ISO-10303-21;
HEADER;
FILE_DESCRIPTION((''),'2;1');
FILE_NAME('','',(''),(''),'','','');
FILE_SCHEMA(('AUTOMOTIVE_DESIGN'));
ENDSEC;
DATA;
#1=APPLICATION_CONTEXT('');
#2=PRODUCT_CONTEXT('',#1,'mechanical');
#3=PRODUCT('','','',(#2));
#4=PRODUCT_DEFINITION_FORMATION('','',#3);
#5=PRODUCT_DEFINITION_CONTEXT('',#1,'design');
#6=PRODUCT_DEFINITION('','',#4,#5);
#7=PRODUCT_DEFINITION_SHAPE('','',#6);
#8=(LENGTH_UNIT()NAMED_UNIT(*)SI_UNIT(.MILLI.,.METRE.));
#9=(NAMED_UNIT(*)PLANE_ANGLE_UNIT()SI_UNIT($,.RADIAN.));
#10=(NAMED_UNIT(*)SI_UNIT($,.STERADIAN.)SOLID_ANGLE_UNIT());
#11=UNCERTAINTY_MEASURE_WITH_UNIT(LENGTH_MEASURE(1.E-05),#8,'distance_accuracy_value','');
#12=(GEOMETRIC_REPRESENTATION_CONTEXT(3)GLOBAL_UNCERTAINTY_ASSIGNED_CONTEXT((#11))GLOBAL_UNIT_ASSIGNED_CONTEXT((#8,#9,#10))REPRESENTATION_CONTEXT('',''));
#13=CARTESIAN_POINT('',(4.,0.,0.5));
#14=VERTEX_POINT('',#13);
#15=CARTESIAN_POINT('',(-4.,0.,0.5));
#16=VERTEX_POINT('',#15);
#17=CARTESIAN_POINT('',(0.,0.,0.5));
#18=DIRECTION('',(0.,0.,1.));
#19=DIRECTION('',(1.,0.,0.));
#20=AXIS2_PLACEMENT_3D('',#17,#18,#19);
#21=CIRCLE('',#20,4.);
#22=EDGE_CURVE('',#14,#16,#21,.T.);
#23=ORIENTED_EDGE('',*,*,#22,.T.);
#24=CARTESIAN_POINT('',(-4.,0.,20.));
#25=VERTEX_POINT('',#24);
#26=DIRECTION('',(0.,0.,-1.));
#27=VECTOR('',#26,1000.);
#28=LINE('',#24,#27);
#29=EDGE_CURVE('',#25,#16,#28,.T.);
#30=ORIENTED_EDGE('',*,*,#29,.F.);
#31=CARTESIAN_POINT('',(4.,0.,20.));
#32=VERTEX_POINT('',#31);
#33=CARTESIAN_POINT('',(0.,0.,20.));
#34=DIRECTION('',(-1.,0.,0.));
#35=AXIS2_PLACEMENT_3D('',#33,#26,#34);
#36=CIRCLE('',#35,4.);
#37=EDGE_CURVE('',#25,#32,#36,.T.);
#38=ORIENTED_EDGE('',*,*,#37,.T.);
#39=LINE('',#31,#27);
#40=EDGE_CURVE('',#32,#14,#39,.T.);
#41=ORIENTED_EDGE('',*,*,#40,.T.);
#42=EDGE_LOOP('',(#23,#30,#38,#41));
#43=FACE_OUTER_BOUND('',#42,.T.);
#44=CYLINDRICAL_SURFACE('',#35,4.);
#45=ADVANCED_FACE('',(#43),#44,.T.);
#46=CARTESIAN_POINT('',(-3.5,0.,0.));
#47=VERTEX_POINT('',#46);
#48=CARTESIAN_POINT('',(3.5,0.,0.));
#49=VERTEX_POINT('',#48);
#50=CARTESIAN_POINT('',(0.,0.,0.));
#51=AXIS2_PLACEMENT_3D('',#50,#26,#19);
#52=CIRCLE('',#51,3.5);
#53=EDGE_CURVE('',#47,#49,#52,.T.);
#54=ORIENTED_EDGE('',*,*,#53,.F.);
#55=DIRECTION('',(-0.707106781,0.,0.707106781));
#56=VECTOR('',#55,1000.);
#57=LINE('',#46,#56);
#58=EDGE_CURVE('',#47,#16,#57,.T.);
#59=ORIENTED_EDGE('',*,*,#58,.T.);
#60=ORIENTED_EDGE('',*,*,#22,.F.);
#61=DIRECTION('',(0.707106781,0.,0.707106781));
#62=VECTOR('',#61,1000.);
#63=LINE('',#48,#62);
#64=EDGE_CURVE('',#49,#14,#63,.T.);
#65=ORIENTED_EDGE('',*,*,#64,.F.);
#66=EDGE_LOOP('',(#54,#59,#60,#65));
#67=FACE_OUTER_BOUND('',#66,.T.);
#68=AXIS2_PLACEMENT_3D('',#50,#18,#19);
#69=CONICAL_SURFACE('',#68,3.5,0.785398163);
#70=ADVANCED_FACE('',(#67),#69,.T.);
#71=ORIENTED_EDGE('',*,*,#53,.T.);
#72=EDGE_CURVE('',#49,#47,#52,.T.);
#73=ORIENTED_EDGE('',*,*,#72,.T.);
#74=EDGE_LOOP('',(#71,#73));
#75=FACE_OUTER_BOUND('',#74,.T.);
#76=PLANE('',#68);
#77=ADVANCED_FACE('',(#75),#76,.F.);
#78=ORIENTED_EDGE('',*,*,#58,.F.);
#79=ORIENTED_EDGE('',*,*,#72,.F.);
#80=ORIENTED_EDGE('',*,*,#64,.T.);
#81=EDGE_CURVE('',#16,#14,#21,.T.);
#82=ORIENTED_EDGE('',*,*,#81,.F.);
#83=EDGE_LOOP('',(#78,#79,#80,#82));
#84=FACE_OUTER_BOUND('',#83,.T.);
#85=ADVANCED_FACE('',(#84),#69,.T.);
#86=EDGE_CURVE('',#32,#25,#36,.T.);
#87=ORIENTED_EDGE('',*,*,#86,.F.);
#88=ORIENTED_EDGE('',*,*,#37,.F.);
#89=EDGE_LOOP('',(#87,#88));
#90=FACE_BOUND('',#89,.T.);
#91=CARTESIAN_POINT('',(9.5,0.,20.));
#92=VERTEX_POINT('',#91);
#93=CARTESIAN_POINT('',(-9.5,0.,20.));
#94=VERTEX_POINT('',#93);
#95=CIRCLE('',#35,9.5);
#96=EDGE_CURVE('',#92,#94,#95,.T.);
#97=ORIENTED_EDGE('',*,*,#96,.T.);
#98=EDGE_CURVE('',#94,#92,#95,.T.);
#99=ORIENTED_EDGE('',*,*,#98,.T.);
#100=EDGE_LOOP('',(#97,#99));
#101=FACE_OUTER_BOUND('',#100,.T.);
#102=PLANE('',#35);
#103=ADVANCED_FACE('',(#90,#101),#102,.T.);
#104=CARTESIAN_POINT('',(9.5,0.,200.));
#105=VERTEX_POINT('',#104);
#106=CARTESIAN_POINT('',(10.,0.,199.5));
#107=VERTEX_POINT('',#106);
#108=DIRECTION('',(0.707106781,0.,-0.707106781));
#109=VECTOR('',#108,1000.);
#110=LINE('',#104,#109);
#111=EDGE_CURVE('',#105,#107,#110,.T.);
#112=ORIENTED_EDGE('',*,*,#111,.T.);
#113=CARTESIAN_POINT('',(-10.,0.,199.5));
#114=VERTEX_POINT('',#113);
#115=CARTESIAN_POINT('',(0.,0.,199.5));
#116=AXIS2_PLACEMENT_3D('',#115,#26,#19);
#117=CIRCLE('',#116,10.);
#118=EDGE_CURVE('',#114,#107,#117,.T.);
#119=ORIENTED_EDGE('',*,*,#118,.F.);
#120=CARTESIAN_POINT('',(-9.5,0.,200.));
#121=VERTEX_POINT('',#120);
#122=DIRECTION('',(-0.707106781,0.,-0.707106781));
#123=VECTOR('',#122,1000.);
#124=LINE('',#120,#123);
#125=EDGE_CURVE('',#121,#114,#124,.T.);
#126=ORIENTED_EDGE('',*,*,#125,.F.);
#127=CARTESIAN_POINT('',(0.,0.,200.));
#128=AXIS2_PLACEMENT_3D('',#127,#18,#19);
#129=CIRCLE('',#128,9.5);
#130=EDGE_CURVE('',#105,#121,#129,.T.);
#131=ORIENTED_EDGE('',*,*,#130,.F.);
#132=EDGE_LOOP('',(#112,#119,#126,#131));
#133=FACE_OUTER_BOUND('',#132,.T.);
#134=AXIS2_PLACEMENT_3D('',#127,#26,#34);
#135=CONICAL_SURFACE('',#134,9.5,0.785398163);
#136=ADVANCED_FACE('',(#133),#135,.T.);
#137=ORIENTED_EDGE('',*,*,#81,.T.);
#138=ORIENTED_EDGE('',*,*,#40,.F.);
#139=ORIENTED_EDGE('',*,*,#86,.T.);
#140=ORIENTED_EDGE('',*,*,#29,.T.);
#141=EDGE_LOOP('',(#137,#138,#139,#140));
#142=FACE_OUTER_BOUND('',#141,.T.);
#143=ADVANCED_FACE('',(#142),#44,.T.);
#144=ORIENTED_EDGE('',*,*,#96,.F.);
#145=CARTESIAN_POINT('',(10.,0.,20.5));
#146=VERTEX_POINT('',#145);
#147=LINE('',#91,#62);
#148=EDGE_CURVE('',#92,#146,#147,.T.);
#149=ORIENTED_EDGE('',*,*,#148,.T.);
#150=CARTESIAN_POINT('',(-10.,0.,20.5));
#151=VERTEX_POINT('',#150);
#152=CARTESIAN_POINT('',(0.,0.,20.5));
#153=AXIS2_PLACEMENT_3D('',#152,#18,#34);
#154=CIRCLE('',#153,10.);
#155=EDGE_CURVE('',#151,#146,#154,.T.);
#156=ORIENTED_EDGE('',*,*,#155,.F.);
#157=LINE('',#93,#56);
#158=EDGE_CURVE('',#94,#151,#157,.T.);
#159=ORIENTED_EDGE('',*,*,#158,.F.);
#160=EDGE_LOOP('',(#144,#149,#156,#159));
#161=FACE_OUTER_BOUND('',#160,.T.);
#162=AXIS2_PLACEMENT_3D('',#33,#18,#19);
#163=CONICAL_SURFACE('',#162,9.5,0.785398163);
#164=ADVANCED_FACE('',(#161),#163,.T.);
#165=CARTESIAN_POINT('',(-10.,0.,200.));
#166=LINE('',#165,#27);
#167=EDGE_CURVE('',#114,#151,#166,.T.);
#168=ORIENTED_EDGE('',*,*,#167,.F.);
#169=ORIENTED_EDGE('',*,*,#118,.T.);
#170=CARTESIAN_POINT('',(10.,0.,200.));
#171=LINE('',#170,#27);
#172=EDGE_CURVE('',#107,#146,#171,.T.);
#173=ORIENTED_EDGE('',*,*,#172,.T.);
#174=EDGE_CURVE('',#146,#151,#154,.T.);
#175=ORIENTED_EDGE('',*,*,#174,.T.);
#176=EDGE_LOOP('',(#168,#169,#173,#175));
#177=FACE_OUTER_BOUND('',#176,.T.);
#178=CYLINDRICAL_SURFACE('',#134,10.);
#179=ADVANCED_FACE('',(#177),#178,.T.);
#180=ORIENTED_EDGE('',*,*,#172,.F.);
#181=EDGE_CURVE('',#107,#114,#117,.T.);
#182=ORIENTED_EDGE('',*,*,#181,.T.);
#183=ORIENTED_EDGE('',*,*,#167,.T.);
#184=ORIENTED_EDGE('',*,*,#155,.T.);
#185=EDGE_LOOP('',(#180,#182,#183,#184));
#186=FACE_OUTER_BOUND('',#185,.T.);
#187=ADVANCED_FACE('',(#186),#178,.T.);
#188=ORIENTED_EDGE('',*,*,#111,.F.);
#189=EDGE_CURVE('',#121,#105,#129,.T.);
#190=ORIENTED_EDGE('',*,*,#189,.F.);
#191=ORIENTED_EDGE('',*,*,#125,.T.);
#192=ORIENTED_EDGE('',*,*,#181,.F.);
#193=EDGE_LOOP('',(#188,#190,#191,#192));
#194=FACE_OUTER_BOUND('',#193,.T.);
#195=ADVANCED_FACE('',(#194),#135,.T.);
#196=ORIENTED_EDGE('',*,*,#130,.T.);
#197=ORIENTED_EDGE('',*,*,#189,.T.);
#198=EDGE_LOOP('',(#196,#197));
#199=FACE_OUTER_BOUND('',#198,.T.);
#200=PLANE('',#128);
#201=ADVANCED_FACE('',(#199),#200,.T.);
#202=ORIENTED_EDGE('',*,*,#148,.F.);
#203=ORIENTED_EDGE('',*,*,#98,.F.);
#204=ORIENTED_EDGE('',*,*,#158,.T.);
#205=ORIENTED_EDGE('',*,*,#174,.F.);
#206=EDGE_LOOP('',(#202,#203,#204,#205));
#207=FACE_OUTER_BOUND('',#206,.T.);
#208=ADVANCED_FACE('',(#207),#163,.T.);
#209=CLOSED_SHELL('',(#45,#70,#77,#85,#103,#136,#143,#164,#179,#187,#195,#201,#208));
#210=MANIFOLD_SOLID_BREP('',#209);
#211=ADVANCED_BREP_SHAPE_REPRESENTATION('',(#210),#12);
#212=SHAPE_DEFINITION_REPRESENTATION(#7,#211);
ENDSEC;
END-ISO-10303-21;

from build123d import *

# Parameters (mm, degrees)
SKETCH_1_R          = 10
EXTRUDE_1_DEPTH     = 200
SKETCH_2_OUTSIDE_W  = 62.398
SKETCH_2_OUTSIDE_H  = 62.398
SKETCH_2_OUTSIDE_R  = 4
CUT_EXTRUDE_1_DEPTH = 20
CHAMFER_1_SIZE      = 0.5


with BuildPart() as part:
    # 草图1 → 凸台-拉伸1 (new body)
    with BuildSketch(Plane.XY):
        Circle(SKETCH_1_R)
    extrude(amount=EXTRUDE_1_DEPTH)

    # 草图2 outside → 切除-拉伸1 (cut)
    with BuildSketch(Plane(origin=(0, 0, 0), x_dir=(-1, 0, 0), z_dir=(0, 0, -1))):
        Rectangle(SKETCH_2_OUTSIDE_W, SKETCH_2_OUTSIDE_H)
        Circle(SKETCH_2_OUTSIDE_R, mode=Mode.SUBTRACT)
    extrude(amount=-CUT_EXTRUDE_1_DEPTH, mode=Mode.SUBTRACT)

    # 倒角1
    chamfer_1_edges = [part.edges().sort_by_distance(p)[0] for p in [
        (4, 0, 0),
        (-10, 0, 200),
        (-10, 0, 20),
    ]]
    chamfer(chamfer_1_edges, length=CHAMFER_1_SIZE)


solid = part.part
